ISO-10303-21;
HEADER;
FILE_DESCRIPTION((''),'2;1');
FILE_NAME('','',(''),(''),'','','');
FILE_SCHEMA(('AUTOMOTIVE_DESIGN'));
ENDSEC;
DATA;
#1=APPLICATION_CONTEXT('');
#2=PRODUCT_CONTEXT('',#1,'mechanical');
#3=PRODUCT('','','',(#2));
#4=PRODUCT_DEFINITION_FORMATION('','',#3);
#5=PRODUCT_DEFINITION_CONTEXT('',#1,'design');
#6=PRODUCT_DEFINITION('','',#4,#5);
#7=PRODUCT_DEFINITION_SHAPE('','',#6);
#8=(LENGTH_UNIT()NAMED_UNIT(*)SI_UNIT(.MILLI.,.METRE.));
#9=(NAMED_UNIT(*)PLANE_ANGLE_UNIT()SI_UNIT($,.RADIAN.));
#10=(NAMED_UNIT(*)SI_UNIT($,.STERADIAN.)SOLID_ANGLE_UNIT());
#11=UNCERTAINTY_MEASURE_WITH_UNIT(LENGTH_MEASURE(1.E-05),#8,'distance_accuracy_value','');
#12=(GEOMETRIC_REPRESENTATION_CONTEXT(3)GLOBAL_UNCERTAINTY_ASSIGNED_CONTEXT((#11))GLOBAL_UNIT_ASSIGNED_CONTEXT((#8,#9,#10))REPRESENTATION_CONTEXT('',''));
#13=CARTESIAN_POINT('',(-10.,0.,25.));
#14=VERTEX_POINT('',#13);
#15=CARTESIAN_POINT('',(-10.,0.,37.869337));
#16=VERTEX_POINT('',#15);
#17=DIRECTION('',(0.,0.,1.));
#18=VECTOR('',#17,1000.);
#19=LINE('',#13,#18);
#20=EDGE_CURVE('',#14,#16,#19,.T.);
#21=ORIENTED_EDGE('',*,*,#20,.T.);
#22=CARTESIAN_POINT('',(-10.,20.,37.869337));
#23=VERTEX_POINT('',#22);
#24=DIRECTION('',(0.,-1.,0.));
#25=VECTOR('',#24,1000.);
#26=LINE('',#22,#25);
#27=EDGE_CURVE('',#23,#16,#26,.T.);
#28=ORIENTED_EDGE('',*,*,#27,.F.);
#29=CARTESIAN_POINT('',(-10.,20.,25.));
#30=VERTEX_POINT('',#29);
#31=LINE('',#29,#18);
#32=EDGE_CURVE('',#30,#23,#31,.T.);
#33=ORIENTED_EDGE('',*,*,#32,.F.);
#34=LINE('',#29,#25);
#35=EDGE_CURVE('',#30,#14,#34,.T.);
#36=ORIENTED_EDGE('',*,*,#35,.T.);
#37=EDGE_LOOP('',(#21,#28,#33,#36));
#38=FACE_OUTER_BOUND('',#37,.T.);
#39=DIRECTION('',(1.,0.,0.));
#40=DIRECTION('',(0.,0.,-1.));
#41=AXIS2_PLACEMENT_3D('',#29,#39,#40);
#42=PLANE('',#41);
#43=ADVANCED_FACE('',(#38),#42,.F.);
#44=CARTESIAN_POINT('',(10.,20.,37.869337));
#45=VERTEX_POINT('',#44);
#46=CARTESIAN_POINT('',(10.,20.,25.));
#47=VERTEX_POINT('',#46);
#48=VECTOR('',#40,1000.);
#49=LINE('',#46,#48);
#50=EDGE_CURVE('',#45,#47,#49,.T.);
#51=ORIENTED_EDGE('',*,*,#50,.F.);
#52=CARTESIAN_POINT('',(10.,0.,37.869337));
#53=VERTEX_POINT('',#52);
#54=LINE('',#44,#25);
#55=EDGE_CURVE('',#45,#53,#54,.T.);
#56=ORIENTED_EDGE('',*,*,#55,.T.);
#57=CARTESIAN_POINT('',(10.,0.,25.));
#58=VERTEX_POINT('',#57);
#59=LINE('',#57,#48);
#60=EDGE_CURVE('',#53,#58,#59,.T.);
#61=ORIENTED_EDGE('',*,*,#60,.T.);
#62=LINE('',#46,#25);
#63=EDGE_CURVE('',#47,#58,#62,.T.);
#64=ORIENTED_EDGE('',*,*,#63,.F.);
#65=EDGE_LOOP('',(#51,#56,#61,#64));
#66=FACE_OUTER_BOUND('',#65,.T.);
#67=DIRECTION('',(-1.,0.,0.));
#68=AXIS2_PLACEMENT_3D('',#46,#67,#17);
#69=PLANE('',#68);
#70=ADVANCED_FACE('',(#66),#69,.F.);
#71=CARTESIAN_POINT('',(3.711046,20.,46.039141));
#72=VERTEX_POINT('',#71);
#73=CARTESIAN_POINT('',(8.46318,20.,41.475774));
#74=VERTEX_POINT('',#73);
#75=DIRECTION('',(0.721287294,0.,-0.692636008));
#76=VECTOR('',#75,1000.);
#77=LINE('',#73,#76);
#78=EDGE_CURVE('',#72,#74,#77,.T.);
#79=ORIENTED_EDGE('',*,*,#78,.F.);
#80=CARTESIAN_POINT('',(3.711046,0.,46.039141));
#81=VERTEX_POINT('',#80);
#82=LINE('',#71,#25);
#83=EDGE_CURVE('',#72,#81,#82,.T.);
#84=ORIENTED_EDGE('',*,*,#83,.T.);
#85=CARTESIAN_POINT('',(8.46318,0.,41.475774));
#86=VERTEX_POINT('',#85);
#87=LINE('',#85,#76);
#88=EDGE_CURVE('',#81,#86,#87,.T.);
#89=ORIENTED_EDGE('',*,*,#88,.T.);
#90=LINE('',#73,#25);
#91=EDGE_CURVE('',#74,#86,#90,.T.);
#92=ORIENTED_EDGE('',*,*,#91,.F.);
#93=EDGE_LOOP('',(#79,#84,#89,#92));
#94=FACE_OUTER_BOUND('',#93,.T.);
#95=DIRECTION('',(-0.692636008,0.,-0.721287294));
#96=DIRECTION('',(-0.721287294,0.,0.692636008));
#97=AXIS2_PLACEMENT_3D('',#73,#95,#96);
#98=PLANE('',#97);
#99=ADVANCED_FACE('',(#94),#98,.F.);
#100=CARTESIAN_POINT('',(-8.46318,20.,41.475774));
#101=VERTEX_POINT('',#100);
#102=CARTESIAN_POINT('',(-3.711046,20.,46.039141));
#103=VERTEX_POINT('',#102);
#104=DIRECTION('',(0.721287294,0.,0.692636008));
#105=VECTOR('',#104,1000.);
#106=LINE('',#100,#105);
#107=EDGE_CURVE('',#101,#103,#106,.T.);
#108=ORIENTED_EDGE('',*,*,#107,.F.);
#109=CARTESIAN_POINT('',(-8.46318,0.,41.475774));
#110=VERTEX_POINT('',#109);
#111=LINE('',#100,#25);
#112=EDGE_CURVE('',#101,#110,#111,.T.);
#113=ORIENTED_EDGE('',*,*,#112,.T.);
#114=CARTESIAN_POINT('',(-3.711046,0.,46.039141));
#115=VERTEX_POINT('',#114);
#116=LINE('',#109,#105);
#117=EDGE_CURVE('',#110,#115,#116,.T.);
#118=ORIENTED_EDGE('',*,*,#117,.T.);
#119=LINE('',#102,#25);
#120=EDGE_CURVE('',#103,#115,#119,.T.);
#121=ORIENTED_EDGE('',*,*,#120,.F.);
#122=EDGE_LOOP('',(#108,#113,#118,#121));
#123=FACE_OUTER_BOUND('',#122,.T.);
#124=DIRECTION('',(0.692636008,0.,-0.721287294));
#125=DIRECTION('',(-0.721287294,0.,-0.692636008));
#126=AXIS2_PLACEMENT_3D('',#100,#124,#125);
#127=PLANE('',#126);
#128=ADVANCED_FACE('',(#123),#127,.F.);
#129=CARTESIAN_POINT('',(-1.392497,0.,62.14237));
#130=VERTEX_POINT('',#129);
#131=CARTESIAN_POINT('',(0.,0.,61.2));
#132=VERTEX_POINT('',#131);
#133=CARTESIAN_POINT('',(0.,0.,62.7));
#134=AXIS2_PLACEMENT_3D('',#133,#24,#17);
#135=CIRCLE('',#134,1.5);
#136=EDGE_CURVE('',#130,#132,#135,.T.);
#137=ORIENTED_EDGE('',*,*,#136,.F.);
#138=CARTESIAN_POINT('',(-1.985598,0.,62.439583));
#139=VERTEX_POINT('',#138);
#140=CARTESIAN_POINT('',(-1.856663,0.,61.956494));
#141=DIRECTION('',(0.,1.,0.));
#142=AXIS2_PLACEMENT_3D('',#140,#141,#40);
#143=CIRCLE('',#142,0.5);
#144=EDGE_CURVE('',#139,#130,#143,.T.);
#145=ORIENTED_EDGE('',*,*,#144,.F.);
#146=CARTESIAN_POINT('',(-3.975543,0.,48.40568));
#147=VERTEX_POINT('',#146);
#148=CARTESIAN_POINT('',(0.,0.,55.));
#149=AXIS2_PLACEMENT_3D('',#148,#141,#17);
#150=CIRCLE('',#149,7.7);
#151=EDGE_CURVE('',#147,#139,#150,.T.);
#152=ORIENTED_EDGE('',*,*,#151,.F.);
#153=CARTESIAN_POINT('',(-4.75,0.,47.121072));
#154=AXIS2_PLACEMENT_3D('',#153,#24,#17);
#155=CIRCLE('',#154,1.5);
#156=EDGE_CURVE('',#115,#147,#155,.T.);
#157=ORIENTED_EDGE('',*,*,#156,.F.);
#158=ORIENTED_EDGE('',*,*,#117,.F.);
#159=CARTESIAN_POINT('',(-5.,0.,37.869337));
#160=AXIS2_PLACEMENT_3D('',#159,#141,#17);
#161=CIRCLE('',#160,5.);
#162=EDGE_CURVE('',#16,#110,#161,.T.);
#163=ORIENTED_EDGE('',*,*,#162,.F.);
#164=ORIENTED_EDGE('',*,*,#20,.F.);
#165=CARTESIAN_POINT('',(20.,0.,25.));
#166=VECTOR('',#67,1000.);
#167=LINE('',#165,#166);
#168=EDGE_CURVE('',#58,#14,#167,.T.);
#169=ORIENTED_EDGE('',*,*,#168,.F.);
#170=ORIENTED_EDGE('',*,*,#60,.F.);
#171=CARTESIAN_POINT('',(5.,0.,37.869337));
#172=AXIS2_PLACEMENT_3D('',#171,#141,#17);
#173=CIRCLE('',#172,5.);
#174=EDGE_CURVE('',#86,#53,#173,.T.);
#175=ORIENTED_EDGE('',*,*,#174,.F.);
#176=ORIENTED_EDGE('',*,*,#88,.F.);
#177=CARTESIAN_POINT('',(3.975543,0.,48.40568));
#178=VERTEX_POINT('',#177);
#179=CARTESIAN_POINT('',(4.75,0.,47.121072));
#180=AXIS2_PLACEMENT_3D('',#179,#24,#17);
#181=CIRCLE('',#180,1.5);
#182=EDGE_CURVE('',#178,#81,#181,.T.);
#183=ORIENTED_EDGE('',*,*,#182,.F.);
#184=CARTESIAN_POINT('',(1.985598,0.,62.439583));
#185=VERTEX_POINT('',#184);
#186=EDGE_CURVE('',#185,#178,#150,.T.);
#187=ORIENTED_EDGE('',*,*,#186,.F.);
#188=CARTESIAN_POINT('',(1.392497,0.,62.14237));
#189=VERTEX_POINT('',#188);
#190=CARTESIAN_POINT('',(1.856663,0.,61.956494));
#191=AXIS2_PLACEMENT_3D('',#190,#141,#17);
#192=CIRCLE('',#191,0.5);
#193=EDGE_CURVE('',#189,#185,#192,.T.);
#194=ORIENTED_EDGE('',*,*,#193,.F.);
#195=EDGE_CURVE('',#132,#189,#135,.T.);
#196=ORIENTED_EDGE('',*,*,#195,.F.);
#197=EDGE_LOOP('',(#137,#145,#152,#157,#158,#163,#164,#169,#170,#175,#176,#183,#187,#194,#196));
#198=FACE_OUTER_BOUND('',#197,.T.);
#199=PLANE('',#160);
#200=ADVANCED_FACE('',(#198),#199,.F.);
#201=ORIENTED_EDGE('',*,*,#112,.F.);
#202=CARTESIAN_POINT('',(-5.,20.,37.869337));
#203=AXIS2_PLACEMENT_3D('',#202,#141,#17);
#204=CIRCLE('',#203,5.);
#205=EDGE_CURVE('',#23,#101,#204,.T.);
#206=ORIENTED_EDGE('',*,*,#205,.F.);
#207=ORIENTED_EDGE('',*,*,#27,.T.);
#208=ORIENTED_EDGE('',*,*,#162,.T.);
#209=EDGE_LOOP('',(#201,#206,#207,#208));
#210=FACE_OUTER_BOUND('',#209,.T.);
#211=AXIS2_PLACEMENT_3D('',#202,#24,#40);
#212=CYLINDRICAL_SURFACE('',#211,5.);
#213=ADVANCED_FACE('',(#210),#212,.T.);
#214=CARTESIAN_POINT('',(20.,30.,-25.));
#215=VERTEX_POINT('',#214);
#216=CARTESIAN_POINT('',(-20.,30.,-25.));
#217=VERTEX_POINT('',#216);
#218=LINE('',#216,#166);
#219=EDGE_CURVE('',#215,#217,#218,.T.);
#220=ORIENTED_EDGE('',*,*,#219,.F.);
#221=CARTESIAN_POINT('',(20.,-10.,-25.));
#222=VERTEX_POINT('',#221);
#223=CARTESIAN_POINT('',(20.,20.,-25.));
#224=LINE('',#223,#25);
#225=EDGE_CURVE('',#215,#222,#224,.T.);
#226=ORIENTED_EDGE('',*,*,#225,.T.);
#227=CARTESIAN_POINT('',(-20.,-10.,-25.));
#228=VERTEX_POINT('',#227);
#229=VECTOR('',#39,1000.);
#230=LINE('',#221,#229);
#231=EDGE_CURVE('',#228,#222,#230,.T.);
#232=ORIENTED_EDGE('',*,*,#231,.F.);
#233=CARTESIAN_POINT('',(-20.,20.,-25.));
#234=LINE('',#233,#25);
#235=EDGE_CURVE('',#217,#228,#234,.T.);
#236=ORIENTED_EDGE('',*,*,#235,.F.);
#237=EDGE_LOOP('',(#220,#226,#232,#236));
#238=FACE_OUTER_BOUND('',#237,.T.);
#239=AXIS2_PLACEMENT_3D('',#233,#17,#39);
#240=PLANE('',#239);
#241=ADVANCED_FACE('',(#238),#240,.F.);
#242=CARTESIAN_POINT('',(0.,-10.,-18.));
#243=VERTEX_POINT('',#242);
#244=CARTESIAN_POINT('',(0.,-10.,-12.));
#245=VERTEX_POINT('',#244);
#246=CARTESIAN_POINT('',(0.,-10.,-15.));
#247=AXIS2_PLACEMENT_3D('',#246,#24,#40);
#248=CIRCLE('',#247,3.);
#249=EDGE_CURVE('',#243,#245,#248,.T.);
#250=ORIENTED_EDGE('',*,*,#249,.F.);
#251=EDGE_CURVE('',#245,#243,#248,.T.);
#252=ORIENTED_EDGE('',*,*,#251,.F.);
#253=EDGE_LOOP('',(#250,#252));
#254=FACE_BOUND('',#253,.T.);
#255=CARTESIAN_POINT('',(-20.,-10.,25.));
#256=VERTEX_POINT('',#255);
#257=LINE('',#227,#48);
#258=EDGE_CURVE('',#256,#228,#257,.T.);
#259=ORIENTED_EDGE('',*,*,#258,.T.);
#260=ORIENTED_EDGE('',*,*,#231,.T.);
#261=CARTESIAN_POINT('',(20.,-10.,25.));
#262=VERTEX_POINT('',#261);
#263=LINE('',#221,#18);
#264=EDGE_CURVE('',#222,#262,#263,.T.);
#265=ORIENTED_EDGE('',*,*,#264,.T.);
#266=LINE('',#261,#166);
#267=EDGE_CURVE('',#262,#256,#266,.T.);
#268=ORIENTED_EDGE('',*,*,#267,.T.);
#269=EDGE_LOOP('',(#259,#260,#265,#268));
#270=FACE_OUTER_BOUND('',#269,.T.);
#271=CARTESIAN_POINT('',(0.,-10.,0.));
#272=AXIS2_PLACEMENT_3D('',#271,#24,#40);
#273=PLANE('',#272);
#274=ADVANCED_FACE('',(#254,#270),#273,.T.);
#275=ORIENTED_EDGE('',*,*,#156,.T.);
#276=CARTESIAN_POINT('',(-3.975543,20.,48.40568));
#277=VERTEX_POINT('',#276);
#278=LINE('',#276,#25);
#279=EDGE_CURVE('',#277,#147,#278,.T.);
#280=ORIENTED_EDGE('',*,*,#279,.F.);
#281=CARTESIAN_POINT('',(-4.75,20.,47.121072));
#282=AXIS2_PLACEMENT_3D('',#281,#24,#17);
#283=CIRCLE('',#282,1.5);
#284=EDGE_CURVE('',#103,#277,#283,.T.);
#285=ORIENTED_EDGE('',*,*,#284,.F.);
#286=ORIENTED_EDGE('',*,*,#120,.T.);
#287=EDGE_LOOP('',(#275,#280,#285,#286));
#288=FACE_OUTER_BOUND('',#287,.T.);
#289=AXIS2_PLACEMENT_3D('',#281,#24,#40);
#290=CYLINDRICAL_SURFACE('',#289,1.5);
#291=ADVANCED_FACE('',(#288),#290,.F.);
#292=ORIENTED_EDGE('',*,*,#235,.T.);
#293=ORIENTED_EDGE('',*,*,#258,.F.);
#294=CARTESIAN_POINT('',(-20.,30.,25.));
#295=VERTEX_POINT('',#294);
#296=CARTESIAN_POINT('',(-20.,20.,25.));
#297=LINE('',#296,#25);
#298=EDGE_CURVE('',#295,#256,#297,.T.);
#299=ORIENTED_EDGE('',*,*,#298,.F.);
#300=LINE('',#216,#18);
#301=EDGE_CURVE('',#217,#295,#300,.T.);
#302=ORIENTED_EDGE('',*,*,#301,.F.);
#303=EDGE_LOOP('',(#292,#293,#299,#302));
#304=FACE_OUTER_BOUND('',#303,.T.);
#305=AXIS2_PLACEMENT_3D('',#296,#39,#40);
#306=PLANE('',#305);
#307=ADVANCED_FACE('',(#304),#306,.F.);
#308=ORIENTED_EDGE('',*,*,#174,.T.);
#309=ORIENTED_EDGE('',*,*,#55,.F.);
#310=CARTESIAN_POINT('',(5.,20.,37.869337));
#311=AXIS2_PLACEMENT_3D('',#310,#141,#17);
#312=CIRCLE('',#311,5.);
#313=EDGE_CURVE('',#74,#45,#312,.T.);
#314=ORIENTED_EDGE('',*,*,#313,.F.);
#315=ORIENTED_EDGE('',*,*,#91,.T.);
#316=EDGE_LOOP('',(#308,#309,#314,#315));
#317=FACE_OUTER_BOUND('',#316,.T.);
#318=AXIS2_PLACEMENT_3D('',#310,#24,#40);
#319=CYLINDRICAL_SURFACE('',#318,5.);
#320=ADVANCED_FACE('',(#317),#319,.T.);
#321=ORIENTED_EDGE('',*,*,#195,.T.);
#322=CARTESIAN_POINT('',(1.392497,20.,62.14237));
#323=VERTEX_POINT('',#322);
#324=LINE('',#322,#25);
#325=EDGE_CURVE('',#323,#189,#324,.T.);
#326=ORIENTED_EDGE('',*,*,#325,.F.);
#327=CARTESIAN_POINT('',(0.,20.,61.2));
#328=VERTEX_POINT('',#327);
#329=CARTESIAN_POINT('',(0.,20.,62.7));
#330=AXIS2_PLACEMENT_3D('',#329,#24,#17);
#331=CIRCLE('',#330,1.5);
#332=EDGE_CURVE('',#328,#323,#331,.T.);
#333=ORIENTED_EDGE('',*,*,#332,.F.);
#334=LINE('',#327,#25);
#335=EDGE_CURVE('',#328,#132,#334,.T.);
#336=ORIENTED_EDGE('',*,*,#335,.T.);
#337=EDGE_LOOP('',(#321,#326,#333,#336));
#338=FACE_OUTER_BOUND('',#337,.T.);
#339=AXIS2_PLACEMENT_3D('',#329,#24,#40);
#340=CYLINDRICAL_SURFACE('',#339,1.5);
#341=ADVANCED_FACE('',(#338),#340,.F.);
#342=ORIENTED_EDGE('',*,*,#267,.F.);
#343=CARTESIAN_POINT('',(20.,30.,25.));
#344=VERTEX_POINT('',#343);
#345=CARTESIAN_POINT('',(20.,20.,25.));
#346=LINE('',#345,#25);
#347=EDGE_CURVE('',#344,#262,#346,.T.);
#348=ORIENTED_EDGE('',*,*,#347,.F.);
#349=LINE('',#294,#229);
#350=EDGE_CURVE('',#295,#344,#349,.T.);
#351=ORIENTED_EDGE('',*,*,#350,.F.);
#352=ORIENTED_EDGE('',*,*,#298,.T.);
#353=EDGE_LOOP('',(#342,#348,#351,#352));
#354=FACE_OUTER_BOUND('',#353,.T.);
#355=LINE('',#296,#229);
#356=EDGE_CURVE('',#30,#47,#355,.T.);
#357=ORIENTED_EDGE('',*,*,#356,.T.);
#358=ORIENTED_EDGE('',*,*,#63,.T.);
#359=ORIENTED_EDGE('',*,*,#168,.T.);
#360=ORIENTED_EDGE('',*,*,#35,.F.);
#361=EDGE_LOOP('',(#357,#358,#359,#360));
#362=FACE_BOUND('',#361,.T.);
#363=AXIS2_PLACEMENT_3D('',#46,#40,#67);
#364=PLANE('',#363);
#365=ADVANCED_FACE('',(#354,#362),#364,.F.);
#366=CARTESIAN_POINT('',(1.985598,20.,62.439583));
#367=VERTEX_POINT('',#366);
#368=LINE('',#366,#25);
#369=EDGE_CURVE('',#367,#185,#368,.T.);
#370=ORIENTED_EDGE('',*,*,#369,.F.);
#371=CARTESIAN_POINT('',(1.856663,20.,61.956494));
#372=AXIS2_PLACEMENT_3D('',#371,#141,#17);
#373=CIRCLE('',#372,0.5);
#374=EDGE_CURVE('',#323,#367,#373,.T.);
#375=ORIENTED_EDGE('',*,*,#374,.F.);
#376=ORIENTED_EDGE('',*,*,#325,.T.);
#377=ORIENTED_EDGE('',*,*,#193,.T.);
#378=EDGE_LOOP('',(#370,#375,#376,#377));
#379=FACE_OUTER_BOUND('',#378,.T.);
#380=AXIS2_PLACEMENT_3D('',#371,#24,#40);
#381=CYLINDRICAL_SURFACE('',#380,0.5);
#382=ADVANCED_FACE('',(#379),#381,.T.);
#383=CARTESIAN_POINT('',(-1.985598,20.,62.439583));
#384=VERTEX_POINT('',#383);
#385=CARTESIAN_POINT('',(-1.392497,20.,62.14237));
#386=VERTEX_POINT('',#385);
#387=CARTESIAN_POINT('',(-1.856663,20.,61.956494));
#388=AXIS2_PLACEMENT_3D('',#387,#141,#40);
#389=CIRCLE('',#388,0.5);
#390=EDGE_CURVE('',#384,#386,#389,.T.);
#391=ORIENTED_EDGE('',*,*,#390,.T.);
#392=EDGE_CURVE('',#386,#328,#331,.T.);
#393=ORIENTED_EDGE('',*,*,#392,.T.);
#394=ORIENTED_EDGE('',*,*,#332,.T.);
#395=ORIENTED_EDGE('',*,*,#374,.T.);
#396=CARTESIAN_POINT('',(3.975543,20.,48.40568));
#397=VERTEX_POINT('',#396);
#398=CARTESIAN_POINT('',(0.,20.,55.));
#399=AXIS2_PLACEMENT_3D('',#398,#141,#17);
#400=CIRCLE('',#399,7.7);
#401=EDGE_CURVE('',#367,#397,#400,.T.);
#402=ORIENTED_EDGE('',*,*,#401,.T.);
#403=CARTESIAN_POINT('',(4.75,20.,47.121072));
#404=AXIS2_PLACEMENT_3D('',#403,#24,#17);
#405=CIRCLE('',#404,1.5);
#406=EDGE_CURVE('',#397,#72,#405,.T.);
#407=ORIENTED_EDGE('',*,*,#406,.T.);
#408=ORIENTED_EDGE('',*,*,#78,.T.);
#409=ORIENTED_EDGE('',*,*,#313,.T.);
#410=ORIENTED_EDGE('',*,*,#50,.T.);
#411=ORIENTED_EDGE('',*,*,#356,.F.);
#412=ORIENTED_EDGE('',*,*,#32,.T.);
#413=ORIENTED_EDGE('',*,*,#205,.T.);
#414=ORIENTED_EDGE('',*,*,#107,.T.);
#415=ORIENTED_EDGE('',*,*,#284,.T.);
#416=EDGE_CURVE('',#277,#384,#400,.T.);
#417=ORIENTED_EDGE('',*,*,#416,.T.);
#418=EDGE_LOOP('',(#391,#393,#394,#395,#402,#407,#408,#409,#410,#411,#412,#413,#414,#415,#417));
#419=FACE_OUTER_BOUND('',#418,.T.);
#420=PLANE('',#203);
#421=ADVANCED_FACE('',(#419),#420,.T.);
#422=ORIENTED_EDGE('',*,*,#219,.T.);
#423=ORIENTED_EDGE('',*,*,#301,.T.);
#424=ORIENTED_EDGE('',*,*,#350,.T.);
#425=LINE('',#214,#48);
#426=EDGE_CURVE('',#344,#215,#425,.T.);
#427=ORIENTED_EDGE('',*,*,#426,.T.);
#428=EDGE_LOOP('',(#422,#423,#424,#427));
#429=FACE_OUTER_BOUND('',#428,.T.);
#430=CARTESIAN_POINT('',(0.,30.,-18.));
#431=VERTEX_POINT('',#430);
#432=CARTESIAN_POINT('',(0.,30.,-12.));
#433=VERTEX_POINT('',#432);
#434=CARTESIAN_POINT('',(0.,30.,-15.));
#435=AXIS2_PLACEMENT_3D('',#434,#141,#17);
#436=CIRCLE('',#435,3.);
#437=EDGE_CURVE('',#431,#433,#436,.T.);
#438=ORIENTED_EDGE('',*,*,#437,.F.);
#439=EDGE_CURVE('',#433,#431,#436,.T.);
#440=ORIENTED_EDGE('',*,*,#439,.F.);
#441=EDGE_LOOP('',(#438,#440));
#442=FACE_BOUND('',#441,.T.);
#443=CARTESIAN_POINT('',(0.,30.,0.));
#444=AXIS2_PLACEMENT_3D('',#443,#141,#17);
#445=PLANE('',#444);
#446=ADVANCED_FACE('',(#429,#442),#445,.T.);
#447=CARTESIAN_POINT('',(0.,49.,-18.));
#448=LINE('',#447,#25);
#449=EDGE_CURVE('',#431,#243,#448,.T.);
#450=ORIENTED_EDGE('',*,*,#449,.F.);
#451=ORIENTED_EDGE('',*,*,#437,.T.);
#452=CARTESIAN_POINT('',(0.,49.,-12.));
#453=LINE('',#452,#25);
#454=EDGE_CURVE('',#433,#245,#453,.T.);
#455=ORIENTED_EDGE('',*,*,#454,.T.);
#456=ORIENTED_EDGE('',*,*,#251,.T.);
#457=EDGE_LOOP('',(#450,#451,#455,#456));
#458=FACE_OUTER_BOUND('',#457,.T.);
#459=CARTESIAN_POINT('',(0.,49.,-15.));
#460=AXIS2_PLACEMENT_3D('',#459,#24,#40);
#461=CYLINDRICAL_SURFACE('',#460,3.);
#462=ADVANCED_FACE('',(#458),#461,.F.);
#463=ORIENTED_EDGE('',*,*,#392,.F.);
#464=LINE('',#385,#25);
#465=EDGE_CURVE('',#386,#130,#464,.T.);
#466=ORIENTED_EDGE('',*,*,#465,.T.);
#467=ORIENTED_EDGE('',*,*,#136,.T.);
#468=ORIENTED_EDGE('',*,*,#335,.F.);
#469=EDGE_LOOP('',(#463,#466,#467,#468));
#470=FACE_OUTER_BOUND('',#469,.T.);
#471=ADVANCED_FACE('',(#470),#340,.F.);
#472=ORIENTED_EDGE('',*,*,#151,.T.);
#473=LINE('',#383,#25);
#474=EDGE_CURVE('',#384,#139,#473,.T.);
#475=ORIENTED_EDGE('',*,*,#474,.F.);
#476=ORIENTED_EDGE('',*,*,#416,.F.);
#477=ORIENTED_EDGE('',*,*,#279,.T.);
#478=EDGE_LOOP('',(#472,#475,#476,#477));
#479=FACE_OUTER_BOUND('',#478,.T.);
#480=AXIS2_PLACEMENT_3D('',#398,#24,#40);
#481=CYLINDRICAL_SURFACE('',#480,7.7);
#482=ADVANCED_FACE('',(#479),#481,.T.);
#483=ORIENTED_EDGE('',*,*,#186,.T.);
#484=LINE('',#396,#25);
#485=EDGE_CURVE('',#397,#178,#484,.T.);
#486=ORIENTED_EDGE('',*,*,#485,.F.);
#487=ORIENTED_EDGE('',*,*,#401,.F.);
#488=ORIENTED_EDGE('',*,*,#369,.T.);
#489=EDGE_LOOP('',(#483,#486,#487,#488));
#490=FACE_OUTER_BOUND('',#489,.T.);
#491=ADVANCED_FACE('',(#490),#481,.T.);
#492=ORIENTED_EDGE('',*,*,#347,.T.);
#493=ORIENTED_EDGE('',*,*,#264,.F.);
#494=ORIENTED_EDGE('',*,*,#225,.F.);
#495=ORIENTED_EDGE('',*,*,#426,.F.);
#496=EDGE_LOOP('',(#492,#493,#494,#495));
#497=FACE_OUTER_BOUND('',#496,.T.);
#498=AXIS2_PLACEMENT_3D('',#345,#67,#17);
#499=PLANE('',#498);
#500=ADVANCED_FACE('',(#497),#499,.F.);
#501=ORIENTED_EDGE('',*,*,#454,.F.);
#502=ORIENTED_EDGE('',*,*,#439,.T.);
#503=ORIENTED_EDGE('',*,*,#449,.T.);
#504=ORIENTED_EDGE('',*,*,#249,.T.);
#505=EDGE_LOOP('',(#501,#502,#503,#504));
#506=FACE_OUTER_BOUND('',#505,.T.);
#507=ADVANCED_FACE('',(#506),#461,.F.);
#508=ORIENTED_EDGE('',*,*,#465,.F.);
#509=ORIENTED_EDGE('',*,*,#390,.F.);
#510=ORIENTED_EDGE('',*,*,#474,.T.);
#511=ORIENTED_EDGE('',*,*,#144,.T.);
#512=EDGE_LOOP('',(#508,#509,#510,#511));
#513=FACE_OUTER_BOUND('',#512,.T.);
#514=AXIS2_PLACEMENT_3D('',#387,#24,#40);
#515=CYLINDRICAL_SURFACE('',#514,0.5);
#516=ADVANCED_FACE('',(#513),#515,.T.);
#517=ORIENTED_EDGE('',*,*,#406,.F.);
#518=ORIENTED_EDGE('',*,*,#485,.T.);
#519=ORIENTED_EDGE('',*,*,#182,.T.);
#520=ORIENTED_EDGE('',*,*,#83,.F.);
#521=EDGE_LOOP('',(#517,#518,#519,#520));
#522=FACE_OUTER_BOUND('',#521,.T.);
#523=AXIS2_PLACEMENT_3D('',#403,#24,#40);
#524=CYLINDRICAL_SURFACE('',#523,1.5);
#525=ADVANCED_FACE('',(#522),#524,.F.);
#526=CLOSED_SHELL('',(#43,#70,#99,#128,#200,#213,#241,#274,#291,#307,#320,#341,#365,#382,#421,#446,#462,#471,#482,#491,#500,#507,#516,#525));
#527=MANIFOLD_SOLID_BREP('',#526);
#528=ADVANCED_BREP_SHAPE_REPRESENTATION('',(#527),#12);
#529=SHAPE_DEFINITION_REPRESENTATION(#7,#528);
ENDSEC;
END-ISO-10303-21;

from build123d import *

# Parameters (mm, degrees)
BOSS_EXTRUDE1_DEPTH = 20
SKETCH2_W           = 40
SKETCH2_H           = 50
BOSS_EXTRUDE2_DEPTH = 10
SKETCH3_W           = 40
SKETCH3_H           = 50
BOSS_EXTRUDE3_DEPTH = 10
SKETCH4_R           = 3
CUT_EXTRUDE1_DEPTH  = 59


with BuildPart() as part:
    # Sketch1 → Boss-Extrude1 (new body)
    with BuildSketch(Plane(origin=(0, 0, 0), x_dir=(1, 0, 0), z_dir=(0, 1, 0))):
        with BuildLine():
            Line((8.463180042, -41.475773732), (3.711045987, -46.039141468))
            ThreePointArc((3.711045987, -46.039141468), (3.259281785, -47.287683344), (3.975543478, -48.405680168))
            ThreePointArc((3.975543478, -48.405680168), (7.623740011, -56.081012602), (1.985598103, -62.439583333))
            ThreePointArc((1.985598103, -62.439583333), (1.632656794, -62.403507094), (1.392497371, -62.14237013))
            ThreePointArc((1.392497371, -62.14237013), (0, -61.2), (-1.392497371, -62.14237013))
            ThreePointArc((-1.392497371, -62.14237013), (-1.632656794, -62.403507094), (-1.985598103, -62.439583333))
            ThreePointArc((-1.985598103, -62.439583333), (-7.623740011, -56.081012602), (-3.975543478, -48.405680168))
            ThreePointArc((-3.975543478, -48.405680168), (-3.259281785, -47.287683344), (-3.711045987, -46.039141468))
            Line((-3.711045987, -46.039141468), (-8.463180042, -41.475773732))
            ThreePointArc((-8.463180042, -41.475773732), (-9.59977718, -39.82945203), (-10, -37.869337265))
            Line((-10, -37.869337265), (-10, -25))
            Line((-10, -25), (-20, -25))
            Line((-20, -25), (-20, 25))
            Line((-20, 25), (20, 25))
            Line((20, 25), (20, -25))
            Line((20, -25), (10, -25))
            Line((10, -25), (10, -37.869337265))
            ThreePointArc((10, -37.869337265), (9.59977718, -39.82945203), (8.463180042, -41.475773732))
        make_face()
    extrude(amount=BOSS_EXTRUDE1_DEPTH)

    # Sketch2 → Boss-Extrude2 (add)
    with BuildSketch(Plane(origin=(0, 20, 0), x_dir=(1, 0, 0), z_dir=(0, 1, 0))):
        Rectangle(SKETCH2_W, SKETCH2_H)
    extrude(amount=BOSS_EXTRUDE2_DEPTH)

    # Sketch3 → Boss-Extrude3 (add)
    with BuildSketch(Plane.XZ):
        Rectangle(SKETCH3_W, SKETCH3_H)
    extrude(amount=BOSS_EXTRUDE3_DEPTH)

    # Sketch4 → Cut-Extrude1 (cut)
    with BuildSketch(Plane.XZ.offset(10)):
        with Locations(Location((0, -15, 0), (0, 0, 270))):
            Circle(SKETCH4_R)
    extrude(amount=-CUT_EXTRUDE1_DEPTH, mode=Mode.SUBTRACT)


solid = part.part
